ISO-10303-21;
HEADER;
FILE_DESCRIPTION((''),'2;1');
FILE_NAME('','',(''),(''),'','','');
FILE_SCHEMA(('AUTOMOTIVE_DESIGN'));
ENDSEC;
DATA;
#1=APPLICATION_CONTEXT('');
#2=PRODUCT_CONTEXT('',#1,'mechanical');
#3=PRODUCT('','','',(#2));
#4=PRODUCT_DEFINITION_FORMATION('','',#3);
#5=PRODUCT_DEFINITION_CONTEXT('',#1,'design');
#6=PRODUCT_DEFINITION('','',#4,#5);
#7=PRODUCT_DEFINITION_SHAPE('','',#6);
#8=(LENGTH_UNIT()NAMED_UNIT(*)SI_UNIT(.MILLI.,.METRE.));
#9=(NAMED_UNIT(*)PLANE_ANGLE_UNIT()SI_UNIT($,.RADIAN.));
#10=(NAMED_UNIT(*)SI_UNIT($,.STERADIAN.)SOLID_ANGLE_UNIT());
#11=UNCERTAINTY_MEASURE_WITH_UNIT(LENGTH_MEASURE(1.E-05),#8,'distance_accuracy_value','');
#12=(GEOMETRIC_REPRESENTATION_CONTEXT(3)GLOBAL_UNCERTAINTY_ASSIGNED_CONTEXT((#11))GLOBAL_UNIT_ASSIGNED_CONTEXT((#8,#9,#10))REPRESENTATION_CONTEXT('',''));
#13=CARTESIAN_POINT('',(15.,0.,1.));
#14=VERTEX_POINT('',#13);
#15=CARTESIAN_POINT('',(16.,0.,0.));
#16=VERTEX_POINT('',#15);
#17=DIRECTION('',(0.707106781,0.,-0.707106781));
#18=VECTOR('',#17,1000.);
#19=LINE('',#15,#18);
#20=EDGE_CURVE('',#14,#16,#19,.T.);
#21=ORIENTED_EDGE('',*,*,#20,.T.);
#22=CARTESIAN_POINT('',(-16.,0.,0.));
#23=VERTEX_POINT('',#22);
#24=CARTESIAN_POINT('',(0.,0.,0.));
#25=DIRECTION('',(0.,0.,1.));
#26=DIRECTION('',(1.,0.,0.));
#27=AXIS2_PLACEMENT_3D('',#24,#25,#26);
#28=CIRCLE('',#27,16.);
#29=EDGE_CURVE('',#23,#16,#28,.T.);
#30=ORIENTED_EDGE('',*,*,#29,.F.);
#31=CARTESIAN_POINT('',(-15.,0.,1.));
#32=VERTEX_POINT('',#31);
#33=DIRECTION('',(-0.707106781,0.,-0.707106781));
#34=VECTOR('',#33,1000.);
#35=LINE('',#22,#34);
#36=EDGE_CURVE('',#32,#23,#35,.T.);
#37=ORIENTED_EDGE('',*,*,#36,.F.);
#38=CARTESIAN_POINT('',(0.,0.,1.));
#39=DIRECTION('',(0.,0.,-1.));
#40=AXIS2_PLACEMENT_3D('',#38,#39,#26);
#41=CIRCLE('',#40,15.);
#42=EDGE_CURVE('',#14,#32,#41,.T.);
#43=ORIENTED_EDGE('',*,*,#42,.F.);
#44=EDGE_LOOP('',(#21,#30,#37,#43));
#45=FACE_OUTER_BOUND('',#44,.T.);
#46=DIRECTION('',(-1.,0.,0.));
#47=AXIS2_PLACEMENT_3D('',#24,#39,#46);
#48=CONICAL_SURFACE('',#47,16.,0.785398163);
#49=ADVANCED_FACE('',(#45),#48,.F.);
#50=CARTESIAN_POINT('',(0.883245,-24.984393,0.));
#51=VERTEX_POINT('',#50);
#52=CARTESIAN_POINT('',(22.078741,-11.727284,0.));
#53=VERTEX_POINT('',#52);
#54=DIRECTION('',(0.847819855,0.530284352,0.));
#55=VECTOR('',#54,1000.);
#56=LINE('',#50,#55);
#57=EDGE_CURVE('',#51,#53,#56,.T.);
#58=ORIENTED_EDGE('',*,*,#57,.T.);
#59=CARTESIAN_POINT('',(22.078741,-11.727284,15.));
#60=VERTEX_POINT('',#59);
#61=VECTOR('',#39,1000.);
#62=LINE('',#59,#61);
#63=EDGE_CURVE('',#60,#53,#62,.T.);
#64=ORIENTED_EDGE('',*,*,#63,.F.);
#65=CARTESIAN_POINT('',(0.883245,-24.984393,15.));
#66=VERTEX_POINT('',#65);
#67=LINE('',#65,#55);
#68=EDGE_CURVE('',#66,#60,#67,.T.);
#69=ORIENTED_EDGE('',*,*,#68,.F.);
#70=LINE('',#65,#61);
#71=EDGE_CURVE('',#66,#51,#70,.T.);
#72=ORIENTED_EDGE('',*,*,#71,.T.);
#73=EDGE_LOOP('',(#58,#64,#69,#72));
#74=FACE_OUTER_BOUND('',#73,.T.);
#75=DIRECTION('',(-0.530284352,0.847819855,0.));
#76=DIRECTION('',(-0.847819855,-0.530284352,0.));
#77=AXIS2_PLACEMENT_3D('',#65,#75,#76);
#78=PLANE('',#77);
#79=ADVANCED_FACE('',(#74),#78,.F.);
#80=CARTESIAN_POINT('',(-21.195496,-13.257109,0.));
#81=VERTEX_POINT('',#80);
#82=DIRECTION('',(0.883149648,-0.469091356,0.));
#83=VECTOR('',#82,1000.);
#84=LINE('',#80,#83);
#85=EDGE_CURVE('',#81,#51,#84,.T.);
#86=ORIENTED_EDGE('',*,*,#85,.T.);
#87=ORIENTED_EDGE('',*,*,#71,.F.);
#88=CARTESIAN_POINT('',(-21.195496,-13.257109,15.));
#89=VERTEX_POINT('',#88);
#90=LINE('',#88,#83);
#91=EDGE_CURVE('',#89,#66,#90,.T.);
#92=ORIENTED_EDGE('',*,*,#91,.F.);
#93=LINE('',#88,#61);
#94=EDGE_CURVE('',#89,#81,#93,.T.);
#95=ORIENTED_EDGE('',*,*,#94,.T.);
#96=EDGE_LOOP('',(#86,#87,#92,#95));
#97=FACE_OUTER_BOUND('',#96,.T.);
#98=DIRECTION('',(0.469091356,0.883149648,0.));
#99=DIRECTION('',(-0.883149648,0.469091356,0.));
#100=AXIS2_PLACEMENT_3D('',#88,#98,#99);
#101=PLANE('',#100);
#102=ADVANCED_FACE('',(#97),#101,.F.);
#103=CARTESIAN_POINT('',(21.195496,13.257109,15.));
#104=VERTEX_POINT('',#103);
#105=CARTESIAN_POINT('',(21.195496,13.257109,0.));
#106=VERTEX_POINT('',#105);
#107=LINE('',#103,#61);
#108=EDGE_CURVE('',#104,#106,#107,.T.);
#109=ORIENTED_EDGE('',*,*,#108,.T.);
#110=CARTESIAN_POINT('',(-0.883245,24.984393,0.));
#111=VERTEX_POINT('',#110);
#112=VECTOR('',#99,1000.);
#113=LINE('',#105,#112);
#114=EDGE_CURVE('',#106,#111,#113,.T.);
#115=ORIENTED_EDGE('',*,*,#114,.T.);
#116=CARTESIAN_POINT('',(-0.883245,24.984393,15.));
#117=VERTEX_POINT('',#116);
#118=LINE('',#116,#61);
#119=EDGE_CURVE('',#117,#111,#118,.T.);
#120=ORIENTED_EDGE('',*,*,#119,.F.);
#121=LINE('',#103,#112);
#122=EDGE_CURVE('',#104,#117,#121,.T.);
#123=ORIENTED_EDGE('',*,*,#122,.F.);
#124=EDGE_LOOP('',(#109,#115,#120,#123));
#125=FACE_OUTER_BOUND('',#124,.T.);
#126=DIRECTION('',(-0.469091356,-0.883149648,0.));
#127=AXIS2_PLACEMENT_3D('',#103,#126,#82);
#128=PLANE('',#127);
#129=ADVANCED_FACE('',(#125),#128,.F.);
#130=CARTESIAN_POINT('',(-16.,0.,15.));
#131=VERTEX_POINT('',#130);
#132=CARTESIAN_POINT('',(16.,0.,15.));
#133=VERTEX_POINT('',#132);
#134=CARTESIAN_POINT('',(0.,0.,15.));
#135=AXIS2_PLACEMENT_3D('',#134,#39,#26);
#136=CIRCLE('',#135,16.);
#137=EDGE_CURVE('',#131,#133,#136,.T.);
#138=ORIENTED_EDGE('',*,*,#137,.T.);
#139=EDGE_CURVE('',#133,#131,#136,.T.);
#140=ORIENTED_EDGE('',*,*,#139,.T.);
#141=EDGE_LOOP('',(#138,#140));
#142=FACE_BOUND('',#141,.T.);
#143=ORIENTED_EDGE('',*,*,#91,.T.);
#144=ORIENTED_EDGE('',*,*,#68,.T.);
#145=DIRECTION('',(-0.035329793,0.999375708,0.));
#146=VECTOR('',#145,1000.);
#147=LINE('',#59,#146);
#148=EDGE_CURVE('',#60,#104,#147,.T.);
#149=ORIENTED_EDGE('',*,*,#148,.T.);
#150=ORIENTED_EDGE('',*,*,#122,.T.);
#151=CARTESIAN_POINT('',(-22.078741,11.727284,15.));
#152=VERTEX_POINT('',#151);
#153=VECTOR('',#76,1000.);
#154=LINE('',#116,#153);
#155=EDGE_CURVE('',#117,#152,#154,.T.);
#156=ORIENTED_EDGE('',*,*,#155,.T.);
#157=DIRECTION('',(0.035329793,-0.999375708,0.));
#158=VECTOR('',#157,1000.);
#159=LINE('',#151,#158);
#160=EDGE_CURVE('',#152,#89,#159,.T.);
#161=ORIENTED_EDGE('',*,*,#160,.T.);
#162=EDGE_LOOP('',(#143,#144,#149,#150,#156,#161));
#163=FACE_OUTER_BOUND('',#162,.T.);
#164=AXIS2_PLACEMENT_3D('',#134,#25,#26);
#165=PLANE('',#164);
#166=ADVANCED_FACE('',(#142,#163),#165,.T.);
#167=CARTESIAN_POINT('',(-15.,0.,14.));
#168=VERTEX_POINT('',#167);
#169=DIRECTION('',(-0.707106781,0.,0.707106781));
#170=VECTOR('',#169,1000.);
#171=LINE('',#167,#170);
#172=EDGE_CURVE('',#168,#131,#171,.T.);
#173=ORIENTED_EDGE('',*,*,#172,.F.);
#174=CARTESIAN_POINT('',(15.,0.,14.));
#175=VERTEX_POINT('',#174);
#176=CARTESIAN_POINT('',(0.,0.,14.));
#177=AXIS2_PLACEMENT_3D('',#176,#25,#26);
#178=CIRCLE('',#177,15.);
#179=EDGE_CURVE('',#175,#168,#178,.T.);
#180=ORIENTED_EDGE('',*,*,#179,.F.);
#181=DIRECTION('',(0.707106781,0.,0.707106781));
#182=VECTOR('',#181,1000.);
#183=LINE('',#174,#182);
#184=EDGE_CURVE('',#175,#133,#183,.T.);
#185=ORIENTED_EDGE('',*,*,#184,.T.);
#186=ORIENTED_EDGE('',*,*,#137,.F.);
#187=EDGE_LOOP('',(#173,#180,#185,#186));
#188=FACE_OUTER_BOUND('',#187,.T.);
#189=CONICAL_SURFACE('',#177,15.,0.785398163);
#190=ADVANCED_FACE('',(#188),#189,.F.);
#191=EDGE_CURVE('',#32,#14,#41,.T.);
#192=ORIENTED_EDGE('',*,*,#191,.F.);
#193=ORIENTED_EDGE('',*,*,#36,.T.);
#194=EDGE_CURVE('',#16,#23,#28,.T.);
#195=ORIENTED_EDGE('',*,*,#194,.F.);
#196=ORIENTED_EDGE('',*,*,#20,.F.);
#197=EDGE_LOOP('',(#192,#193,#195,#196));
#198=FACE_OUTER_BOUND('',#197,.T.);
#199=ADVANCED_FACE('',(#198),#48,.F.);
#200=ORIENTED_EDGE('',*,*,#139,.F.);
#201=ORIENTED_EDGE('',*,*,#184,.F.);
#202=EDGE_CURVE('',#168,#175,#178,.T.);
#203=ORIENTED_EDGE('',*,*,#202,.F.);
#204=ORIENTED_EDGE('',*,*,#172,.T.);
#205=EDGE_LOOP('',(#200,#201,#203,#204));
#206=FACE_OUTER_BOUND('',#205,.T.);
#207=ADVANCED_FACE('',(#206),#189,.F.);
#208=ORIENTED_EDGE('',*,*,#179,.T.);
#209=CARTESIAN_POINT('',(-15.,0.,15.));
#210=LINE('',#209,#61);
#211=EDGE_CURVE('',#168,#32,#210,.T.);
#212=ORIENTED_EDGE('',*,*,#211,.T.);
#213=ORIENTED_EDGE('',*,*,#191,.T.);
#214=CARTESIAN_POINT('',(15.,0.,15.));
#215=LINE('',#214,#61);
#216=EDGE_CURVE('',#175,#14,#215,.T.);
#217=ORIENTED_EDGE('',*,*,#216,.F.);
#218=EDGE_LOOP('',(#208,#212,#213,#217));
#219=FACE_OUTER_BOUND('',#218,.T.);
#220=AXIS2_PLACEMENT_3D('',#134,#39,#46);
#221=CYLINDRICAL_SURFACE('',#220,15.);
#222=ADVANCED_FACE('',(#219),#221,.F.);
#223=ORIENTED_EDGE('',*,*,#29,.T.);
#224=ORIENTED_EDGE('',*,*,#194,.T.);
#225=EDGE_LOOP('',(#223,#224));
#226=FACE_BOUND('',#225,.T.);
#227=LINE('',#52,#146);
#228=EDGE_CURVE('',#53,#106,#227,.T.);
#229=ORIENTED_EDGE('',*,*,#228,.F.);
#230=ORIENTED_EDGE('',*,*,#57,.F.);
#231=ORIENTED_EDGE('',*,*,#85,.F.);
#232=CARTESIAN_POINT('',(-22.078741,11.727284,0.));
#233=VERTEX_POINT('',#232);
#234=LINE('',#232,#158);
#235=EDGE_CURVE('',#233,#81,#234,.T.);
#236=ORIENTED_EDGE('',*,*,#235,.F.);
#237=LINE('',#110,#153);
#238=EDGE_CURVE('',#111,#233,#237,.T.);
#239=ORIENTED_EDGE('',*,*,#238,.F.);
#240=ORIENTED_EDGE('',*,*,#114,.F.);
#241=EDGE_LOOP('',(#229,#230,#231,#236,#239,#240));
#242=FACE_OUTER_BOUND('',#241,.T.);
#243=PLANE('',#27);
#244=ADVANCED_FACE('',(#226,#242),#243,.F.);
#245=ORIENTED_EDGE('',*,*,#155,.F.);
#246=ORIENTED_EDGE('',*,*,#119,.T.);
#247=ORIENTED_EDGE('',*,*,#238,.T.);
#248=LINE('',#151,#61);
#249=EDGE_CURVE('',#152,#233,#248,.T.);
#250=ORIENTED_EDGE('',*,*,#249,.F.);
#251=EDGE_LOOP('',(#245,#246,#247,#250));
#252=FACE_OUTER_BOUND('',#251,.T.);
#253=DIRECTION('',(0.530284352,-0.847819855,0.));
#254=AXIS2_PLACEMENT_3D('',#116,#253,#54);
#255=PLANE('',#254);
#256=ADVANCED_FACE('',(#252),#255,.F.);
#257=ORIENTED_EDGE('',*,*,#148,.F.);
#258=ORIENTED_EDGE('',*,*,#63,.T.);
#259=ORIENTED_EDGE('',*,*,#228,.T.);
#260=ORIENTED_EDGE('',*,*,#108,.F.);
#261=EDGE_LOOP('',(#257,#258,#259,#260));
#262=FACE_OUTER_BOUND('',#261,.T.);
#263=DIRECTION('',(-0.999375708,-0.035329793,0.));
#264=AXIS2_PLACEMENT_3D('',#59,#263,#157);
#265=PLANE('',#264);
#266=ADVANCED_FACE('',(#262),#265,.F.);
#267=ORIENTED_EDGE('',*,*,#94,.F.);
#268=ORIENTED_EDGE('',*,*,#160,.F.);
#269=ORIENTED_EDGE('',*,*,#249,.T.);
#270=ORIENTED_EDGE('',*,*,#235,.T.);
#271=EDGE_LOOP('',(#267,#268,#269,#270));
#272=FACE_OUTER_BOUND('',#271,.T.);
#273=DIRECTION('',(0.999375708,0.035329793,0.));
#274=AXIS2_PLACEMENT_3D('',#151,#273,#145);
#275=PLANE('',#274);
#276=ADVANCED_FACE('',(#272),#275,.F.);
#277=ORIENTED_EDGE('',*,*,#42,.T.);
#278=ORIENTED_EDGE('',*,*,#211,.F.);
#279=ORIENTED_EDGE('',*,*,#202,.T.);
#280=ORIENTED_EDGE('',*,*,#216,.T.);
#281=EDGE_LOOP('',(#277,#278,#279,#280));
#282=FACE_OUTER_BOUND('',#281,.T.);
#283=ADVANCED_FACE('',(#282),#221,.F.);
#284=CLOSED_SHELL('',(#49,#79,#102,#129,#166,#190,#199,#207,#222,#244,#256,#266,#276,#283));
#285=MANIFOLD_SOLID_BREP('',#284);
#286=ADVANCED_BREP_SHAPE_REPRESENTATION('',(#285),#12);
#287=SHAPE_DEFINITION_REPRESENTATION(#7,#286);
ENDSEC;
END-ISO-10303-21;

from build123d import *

# Parameters (mm, degrees)
SKETCH1_R           = 15
BOSS_EXTRUDE1_DEPTH = 15
CHAMFER1_SIZE       = 1


with BuildPart() as part:
    # Sketch1 → Boss-Extrude1 (new body)
    with BuildSketch(Plane.XY):
        Polygon((22.078741188, -11.727283895), (21.195496365, 13.257108805), (-0.883244823, 24.9843927), (-22.078741188, 11.727283895), (-21.195496365, -13.257108805), (0.883244823, -24.9843927), align=None)
        Circle(SKETCH1_R, mode=Mode.SUBTRACT)
    extrude(amount=BOSS_EXTRUDE1_DEPTH)

    # Chamfer1
    chamfer1_edges = [part.edges().sort_by_distance(p)[0] for p in [
        (-15, 0, 0),
        (-15, 0, 15),
    ]]
    chamfer(chamfer1_edges, length=CHAMFER1_SIZE)


solid = part.part
